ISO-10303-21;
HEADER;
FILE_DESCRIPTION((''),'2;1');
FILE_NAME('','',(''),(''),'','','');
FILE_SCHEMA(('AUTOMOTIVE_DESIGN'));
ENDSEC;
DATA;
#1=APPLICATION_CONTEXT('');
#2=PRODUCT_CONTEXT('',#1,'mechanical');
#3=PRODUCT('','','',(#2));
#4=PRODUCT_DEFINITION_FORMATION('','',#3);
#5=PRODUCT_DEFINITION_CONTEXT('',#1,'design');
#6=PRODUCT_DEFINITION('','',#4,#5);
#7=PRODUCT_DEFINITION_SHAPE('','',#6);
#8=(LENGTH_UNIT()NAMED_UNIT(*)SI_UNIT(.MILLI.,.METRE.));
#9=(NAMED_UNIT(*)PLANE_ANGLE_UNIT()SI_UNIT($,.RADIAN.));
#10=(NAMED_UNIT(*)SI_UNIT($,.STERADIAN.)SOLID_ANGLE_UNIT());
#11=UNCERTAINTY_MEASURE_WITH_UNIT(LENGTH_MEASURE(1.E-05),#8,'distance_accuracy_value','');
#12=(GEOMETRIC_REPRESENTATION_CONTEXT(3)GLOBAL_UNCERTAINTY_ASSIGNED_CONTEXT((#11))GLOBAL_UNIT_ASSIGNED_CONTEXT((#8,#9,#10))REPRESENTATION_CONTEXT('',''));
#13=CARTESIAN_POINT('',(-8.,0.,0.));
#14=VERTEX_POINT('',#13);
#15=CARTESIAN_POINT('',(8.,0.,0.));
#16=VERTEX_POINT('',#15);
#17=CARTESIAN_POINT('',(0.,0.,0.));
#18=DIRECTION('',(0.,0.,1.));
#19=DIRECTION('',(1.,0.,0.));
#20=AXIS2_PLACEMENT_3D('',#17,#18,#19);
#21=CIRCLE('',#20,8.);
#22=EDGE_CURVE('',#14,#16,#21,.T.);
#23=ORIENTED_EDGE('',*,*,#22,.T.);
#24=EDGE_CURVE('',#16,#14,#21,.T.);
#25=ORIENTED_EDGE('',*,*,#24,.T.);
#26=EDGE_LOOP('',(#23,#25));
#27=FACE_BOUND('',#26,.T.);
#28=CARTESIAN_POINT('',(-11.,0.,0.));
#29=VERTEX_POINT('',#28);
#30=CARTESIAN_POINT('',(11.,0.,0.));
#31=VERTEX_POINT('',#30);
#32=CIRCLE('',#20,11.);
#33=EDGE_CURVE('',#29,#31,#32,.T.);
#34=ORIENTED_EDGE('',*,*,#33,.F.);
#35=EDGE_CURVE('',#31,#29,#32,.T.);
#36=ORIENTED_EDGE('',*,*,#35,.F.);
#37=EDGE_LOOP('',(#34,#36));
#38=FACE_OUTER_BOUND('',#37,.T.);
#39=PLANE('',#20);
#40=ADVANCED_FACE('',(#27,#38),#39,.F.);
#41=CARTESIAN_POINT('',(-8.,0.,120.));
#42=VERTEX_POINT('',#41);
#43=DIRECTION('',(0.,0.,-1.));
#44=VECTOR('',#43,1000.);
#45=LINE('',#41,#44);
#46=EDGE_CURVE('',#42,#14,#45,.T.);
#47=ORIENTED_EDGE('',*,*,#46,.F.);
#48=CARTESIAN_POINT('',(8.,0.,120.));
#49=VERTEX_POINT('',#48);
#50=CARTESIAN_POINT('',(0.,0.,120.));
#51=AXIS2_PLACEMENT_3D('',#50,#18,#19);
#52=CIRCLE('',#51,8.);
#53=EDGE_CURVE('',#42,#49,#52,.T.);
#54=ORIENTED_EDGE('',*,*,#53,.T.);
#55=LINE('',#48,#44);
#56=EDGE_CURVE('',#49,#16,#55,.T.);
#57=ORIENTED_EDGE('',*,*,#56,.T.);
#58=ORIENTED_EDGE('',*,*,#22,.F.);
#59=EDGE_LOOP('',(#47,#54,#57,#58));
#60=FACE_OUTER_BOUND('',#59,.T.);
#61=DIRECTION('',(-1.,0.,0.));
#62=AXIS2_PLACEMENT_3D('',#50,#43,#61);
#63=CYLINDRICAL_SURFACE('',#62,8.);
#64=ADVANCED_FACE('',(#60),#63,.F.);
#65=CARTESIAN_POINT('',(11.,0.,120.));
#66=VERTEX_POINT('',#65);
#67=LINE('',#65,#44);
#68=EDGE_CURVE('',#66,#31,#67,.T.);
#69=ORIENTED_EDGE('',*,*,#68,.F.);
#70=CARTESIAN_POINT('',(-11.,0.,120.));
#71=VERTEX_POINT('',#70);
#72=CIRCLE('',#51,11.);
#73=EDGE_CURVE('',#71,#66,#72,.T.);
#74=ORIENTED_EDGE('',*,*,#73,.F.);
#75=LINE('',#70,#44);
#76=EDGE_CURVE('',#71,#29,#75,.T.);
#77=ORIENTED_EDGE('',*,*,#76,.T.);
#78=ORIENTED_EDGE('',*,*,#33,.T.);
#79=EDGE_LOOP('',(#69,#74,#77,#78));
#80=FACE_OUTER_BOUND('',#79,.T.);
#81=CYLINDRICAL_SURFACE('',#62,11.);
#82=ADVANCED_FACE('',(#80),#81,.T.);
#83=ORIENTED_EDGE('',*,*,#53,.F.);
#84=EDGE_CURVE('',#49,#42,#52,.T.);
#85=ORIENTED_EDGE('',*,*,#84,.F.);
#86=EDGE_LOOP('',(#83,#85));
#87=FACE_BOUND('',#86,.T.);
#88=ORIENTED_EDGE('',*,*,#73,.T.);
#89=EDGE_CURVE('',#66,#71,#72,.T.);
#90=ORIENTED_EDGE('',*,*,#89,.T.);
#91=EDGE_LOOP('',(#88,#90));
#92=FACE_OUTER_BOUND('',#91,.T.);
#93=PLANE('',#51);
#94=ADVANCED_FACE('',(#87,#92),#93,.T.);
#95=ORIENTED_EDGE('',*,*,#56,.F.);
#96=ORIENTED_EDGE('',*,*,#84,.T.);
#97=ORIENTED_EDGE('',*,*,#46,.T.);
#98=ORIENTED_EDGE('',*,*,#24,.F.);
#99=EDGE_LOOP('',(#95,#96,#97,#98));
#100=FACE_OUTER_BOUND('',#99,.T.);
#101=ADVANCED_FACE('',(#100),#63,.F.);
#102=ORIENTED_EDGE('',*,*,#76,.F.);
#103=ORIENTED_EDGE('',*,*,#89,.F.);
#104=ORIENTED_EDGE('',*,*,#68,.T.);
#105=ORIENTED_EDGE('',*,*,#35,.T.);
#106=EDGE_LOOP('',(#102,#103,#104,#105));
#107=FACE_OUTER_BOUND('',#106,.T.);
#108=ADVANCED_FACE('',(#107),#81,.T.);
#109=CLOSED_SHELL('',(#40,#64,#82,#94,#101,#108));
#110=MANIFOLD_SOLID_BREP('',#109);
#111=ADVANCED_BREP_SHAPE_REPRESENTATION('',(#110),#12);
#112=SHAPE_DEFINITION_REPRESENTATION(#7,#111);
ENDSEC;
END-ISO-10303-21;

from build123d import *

# Parameters (mm, degrees)
SKETCH_1_R           = 11
SKETCH_1_R_2         = 8
BOSS_EXTRUDE_1_DEPTH = 120


with BuildPart() as part:
    # Sketch 1 → Boss-Extrude 1 (new body)
    with BuildSketch(Plane.XY):
        Circle(SKETCH_1_R)
        Circle(SKETCH_1_R_2, mode=Mode.SUBTRACT)
    extrude(amount=BOSS_EXTRUDE_1_DEPTH)


solid = part.part
